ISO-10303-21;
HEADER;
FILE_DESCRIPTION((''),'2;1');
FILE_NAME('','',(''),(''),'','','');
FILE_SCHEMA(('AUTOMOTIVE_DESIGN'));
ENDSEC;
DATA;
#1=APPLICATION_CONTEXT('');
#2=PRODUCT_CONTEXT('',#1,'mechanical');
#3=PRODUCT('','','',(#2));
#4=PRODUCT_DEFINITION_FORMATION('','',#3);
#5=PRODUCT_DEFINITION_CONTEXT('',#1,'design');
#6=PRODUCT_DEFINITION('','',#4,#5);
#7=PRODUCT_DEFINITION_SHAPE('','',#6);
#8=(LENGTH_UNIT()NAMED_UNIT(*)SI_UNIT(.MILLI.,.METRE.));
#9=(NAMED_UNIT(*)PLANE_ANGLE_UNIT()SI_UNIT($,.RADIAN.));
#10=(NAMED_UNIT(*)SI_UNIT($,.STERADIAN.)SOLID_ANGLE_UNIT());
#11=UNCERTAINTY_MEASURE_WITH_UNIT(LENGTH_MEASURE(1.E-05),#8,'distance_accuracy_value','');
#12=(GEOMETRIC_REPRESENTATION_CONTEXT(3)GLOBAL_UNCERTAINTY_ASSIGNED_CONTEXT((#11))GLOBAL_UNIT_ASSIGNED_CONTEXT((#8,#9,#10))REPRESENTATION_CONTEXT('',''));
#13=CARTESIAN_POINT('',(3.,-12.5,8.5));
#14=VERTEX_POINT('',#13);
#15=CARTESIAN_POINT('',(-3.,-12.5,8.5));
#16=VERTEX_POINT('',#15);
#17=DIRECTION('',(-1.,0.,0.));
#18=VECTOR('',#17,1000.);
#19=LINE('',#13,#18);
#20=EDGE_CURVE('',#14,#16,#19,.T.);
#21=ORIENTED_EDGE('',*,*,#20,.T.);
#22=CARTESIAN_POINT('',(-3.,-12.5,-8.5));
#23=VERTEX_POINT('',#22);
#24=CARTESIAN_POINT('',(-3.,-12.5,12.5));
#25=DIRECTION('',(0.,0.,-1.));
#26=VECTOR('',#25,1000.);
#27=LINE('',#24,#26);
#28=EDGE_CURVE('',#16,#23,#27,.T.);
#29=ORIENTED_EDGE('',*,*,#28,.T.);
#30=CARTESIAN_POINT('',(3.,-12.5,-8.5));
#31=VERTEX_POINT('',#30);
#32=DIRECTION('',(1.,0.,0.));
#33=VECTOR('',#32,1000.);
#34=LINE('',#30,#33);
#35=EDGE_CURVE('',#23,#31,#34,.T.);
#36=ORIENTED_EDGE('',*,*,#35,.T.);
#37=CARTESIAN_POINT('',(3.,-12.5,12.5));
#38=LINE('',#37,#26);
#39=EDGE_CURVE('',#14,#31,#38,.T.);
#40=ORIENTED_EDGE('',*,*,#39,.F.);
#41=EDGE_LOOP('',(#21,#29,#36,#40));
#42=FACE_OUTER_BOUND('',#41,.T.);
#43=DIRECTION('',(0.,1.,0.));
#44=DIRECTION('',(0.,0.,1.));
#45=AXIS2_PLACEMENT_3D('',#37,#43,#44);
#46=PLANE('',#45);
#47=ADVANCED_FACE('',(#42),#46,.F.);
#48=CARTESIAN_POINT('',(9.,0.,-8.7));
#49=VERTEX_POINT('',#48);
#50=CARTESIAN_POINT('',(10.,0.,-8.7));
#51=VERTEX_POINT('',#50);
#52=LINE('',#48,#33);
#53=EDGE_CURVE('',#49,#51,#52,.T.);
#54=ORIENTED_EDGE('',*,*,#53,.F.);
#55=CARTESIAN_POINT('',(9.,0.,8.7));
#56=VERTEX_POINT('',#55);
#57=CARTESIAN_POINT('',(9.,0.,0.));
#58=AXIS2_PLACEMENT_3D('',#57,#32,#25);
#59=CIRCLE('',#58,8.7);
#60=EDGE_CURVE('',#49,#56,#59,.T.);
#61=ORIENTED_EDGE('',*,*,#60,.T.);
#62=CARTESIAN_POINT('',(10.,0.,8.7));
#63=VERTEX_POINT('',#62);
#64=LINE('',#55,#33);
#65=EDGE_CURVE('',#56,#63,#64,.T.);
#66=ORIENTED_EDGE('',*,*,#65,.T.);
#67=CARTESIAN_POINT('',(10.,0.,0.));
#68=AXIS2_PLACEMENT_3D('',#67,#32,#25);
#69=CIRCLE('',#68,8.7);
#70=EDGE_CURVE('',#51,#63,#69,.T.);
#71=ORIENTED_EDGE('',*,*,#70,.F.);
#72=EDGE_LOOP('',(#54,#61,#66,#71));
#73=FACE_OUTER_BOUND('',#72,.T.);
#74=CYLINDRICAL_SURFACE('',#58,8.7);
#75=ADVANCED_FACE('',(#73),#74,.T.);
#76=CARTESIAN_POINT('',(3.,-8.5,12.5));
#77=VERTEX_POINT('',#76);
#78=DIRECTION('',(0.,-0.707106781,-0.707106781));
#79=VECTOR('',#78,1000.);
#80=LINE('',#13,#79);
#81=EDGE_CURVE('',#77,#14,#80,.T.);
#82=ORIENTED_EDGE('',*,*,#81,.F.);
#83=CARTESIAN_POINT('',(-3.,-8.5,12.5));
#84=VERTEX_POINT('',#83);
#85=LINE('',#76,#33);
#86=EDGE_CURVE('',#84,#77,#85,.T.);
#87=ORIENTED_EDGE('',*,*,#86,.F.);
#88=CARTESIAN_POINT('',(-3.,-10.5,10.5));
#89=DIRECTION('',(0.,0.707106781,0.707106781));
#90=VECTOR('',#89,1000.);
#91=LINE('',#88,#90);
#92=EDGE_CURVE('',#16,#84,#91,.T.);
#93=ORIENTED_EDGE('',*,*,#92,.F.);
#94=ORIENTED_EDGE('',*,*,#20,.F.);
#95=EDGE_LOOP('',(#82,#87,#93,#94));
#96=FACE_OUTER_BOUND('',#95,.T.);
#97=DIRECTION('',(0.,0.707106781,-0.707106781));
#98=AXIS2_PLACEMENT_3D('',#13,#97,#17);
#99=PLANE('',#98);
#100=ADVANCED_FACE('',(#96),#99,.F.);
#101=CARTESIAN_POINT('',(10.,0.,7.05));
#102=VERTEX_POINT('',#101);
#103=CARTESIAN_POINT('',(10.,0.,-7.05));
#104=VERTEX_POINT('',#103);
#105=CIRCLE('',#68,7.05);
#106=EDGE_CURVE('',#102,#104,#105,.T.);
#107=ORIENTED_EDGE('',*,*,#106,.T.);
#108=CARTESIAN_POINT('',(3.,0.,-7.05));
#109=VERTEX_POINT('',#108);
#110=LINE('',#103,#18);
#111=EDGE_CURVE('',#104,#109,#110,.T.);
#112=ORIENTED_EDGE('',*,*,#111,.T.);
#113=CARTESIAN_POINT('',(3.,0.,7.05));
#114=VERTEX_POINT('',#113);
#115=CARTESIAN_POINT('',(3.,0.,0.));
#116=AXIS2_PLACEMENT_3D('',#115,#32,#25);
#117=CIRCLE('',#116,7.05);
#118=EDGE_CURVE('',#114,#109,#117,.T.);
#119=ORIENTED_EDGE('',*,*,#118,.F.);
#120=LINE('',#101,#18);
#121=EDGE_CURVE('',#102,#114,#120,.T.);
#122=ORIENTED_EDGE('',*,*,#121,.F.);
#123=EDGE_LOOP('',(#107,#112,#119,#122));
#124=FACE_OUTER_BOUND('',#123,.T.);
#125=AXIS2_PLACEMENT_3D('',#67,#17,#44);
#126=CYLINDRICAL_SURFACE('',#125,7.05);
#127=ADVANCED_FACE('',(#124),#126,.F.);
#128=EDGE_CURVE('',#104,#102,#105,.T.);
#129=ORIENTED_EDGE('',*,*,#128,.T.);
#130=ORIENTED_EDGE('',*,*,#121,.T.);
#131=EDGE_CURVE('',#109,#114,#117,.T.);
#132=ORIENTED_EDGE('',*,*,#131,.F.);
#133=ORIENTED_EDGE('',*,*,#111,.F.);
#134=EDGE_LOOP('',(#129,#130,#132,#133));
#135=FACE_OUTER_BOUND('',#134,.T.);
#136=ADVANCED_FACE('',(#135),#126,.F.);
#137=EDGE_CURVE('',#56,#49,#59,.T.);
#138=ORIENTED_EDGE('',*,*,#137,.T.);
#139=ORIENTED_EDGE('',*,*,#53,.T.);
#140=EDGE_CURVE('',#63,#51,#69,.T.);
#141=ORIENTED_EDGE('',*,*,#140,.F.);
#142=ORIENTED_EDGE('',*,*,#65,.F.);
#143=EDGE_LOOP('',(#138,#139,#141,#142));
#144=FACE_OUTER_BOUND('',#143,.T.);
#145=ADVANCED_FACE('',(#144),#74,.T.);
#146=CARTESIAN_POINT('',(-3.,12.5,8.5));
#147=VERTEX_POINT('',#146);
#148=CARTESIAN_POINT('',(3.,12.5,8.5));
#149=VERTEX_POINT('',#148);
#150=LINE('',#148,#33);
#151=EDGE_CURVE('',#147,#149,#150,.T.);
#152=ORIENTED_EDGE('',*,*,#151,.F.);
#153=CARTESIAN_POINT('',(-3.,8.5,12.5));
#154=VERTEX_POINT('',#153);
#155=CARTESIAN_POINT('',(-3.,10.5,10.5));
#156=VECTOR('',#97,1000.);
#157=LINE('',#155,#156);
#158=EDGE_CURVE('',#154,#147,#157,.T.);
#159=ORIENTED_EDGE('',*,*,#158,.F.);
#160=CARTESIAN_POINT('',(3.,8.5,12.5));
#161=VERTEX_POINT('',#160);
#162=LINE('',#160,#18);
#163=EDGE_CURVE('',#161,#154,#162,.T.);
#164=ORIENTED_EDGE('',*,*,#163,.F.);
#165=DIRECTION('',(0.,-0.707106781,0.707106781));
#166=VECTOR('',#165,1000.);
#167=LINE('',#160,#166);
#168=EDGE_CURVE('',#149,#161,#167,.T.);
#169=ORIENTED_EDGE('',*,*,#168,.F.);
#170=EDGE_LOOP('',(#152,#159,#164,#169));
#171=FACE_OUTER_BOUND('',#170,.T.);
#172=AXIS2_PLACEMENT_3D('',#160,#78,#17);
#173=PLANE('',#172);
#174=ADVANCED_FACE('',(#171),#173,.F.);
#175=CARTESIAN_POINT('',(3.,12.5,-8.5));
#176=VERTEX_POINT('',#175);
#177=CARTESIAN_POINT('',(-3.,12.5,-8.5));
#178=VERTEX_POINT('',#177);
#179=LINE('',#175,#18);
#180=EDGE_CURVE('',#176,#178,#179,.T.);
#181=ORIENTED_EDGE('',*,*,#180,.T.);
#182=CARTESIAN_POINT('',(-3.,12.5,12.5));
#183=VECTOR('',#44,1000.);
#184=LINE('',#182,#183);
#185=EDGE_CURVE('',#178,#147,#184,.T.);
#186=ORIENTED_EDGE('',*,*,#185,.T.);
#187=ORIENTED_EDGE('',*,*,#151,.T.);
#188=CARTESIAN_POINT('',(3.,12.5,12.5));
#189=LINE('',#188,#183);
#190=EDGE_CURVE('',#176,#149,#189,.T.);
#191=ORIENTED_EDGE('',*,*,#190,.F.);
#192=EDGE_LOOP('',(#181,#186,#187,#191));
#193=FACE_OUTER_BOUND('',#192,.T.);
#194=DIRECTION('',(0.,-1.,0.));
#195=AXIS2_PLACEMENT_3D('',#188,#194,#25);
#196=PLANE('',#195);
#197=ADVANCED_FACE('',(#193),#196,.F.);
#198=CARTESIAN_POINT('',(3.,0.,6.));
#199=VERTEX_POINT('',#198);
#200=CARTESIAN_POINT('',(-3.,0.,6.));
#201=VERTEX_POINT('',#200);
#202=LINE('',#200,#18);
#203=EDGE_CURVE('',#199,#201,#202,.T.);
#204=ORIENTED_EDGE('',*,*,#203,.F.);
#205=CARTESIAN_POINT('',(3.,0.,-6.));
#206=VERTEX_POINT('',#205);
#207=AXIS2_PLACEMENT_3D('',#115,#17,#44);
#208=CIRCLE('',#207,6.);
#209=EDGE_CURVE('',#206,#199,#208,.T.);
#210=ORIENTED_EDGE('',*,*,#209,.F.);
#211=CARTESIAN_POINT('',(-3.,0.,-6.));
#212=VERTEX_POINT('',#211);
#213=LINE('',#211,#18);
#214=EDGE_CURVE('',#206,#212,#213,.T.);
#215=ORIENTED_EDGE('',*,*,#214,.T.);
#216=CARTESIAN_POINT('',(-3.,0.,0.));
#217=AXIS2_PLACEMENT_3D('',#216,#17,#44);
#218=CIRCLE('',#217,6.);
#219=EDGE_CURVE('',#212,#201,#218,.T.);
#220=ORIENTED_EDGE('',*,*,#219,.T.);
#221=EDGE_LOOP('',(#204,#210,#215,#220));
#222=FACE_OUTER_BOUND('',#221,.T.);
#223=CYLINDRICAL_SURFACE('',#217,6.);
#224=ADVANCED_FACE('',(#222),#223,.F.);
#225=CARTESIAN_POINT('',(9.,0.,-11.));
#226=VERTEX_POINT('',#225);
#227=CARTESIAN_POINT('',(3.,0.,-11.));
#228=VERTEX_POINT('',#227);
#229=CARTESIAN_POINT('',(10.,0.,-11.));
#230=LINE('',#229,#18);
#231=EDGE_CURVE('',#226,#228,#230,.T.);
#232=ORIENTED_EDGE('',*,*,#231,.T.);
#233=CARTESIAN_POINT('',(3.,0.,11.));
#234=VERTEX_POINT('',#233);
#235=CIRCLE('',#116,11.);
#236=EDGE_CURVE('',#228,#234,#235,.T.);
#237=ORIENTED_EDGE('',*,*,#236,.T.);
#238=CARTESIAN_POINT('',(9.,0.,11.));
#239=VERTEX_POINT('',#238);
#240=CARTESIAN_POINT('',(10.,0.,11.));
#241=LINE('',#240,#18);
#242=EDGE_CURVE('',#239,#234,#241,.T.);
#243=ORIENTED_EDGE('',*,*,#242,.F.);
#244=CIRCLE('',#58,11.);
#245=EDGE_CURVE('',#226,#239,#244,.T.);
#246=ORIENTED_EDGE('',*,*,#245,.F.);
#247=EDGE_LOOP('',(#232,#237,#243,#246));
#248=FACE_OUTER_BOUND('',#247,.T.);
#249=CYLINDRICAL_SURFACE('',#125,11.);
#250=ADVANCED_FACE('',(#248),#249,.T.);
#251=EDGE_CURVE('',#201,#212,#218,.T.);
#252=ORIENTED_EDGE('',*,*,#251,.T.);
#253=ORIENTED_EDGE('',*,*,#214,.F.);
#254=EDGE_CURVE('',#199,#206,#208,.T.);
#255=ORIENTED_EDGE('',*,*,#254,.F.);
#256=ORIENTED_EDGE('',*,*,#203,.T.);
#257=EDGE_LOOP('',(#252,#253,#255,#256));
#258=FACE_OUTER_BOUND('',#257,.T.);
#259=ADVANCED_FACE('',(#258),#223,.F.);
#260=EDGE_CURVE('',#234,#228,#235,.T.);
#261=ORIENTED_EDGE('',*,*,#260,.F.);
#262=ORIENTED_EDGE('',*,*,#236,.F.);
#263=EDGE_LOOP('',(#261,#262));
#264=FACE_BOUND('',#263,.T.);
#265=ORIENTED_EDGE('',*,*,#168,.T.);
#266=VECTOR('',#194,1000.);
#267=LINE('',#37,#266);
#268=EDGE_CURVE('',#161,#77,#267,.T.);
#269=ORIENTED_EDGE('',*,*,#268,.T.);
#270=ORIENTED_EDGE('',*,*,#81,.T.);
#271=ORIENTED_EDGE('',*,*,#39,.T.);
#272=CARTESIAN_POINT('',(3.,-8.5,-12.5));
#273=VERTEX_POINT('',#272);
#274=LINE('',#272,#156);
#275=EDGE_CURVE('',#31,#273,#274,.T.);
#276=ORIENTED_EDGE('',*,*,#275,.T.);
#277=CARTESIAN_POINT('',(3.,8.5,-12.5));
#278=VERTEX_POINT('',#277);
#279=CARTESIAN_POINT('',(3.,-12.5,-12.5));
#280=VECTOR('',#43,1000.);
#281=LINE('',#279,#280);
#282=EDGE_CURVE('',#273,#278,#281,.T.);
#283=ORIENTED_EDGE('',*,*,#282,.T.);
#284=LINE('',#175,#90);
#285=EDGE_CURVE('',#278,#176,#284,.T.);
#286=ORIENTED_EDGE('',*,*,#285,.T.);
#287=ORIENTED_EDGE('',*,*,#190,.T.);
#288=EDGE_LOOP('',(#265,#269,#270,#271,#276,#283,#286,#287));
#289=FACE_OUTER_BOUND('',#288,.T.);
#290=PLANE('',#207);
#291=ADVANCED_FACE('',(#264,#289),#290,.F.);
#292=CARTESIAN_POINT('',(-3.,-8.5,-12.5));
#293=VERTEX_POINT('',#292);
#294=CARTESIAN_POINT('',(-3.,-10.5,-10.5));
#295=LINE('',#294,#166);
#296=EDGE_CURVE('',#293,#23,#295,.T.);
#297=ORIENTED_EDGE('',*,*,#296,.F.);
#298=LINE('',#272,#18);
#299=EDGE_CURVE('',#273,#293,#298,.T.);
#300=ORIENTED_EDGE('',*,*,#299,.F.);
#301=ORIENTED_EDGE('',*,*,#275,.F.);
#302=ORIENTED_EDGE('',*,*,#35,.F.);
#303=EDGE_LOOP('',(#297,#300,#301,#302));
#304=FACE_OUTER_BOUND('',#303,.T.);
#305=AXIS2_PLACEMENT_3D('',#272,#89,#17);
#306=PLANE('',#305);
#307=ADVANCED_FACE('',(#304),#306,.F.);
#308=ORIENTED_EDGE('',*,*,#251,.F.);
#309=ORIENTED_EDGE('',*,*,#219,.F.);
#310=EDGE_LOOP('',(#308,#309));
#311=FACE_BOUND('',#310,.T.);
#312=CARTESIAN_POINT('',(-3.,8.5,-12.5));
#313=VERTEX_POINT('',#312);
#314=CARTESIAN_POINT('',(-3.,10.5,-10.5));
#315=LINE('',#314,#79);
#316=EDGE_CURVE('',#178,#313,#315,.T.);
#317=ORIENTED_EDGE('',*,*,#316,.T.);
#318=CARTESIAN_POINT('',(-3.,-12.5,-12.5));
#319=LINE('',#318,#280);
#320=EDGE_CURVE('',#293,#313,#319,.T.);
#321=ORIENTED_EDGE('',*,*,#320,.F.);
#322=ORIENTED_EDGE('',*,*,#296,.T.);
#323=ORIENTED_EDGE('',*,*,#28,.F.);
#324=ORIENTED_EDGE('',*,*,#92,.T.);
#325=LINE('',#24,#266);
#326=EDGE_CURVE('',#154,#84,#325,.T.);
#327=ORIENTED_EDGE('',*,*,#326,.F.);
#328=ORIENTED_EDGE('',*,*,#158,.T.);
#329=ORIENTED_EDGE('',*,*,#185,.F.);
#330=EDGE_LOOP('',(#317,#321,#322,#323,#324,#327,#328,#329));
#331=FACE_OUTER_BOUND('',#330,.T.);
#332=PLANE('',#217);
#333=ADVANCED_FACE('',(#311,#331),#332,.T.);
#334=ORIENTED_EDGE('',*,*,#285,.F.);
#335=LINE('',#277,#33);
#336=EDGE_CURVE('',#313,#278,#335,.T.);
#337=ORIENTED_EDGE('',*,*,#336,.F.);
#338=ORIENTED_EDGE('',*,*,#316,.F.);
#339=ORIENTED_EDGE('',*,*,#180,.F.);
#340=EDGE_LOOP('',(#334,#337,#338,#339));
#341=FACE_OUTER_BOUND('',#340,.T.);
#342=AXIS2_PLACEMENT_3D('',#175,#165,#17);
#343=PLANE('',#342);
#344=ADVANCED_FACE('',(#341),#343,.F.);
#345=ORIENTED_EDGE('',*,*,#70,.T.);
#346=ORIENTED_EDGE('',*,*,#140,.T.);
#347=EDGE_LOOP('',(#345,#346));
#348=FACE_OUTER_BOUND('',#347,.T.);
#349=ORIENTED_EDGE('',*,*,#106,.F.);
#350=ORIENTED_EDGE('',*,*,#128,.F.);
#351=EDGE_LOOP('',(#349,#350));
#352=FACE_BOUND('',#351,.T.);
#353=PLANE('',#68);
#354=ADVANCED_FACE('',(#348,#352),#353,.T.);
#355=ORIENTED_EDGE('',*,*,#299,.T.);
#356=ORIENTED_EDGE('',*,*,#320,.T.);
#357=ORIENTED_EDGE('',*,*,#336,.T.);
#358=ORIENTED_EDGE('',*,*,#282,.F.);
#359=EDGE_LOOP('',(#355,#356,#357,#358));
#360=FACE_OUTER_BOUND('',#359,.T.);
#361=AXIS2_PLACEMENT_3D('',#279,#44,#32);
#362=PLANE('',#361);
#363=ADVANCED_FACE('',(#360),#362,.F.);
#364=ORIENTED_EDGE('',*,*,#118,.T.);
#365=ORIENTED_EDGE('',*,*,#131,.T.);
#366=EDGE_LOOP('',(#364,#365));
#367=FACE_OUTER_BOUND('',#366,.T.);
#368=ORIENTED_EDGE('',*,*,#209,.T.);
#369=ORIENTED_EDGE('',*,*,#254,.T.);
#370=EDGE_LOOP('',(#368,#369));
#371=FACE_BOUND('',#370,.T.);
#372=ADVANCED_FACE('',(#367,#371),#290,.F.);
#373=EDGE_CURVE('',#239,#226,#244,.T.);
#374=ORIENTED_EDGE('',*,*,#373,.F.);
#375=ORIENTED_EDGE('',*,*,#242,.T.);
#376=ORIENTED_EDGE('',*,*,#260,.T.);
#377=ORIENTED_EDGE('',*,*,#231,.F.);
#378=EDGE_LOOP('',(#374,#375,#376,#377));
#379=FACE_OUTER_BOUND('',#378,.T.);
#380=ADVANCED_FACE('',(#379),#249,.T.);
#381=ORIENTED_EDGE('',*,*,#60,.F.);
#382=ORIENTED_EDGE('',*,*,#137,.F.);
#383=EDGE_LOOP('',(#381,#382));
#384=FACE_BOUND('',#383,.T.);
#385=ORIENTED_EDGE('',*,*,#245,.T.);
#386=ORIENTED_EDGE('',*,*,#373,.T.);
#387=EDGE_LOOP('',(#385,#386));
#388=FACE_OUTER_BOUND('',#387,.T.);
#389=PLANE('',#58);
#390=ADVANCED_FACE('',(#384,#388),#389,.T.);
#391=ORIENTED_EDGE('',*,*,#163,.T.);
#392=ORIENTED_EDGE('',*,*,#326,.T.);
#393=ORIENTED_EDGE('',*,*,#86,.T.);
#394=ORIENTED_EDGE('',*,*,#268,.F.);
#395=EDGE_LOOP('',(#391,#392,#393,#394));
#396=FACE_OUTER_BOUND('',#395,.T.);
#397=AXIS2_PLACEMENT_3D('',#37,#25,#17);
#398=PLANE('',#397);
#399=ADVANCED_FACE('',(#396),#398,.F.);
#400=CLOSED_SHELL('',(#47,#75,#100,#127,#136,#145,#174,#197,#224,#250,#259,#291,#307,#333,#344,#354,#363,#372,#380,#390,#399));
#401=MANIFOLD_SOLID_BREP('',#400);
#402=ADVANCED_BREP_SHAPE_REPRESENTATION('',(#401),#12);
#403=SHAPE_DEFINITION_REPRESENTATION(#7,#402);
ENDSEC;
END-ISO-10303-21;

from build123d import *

# Parameters (mm, degrees)
SKETCH1_W              = 25
SKETCH1_H              = 25
BOSS_EXTRUDE1_DEPTH    = 3
M14_TAPPED_HOLE1_D     = 12
M14_TAPPED_HOLE1_DEPTH = 34
M14_TAPPED_HOLE1_TIP   = 3.605163714
SKETCH5_R              = 11
SKETCH5_R_2            = 7.05
BOSS_EXTRUDE2_DEPTH    = 7
CUT_EXTRUDE1_START     = -1
SKETCH6_R              = 11
SKETCH6_R_2            = 8.7
CUT_EXTRUDE1_DEPTH     = 1
CHAMFER1_SIZE          = 4


with BuildPart() as part:
    # Sketch1 → Boss-Extrude1 (new, symmetric)
    with BuildSketch(Plane(origin=(0, 0, 0), x_dir=(0, 0, -1), z_dir=(1, 0, 0))):
        Rectangle(SKETCH1_W, SKETCH1_H)
    extrude(amount=BOSS_EXTRUDE1_DEPTH, both=True)

    # M14 Tapped Hole1
    with Locations(Plane.ZY.offset(3)):
        with Locations((0, 0)):
            Hole(M14_TAPPED_HOLE1_D / 2, depth=M14_TAPPED_HOLE1_DEPTH)
            with Locations((0, 0, -(M14_TAPPED_HOLE1_DEPTH + M14_TAPPED_HOLE1_TIP / 2))):  # 118° drill point
                Cone(0, M14_TAPPED_HOLE1_D / 2, M14_TAPPED_HOLE1_TIP, mode=Mode.SUBTRACT)

    # Sketch5 → Boss-Extrude2 (add)
    with BuildSketch(Plane(origin=(3, 0, 0), x_dir=(0, 0, -1), z_dir=(1, 0, 0))):
        Circle(SKETCH5_R)
        Circle(SKETCH5_R_2, mode=Mode.SUBTRACT)
    extrude(amount=BOSS_EXTRUDE2_DEPTH)

    # Sketch6 → Cut-Extrude1 (cut)
    with BuildSketch(Plane(origin=(10, 0, 0), x_dir=(0, 0, -1), z_dir=(1, 0, 0)).offset(CUT_EXTRUDE1_START)):
        Circle(SKETCH6_R)
        Circle(SKETCH6_R_2, mode=Mode.SUBTRACT)
    extrude(amount=CUT_EXTRUDE1_DEPTH, mode=Mode.SUBTRACT)

    # Chamfer1
    chamfer1_edges = [part.edges().sort_by_distance(p)[0] for p in [
        (0, -12.5, -12.5),
        (0, -12.5, 12.5),
        (0, 12.5, 12.5),
        (0, 12.5, -12.5),
    ]]
    chamfer(chamfer1_edges, length=CHAMFER1_SIZE)


solid = part.part
